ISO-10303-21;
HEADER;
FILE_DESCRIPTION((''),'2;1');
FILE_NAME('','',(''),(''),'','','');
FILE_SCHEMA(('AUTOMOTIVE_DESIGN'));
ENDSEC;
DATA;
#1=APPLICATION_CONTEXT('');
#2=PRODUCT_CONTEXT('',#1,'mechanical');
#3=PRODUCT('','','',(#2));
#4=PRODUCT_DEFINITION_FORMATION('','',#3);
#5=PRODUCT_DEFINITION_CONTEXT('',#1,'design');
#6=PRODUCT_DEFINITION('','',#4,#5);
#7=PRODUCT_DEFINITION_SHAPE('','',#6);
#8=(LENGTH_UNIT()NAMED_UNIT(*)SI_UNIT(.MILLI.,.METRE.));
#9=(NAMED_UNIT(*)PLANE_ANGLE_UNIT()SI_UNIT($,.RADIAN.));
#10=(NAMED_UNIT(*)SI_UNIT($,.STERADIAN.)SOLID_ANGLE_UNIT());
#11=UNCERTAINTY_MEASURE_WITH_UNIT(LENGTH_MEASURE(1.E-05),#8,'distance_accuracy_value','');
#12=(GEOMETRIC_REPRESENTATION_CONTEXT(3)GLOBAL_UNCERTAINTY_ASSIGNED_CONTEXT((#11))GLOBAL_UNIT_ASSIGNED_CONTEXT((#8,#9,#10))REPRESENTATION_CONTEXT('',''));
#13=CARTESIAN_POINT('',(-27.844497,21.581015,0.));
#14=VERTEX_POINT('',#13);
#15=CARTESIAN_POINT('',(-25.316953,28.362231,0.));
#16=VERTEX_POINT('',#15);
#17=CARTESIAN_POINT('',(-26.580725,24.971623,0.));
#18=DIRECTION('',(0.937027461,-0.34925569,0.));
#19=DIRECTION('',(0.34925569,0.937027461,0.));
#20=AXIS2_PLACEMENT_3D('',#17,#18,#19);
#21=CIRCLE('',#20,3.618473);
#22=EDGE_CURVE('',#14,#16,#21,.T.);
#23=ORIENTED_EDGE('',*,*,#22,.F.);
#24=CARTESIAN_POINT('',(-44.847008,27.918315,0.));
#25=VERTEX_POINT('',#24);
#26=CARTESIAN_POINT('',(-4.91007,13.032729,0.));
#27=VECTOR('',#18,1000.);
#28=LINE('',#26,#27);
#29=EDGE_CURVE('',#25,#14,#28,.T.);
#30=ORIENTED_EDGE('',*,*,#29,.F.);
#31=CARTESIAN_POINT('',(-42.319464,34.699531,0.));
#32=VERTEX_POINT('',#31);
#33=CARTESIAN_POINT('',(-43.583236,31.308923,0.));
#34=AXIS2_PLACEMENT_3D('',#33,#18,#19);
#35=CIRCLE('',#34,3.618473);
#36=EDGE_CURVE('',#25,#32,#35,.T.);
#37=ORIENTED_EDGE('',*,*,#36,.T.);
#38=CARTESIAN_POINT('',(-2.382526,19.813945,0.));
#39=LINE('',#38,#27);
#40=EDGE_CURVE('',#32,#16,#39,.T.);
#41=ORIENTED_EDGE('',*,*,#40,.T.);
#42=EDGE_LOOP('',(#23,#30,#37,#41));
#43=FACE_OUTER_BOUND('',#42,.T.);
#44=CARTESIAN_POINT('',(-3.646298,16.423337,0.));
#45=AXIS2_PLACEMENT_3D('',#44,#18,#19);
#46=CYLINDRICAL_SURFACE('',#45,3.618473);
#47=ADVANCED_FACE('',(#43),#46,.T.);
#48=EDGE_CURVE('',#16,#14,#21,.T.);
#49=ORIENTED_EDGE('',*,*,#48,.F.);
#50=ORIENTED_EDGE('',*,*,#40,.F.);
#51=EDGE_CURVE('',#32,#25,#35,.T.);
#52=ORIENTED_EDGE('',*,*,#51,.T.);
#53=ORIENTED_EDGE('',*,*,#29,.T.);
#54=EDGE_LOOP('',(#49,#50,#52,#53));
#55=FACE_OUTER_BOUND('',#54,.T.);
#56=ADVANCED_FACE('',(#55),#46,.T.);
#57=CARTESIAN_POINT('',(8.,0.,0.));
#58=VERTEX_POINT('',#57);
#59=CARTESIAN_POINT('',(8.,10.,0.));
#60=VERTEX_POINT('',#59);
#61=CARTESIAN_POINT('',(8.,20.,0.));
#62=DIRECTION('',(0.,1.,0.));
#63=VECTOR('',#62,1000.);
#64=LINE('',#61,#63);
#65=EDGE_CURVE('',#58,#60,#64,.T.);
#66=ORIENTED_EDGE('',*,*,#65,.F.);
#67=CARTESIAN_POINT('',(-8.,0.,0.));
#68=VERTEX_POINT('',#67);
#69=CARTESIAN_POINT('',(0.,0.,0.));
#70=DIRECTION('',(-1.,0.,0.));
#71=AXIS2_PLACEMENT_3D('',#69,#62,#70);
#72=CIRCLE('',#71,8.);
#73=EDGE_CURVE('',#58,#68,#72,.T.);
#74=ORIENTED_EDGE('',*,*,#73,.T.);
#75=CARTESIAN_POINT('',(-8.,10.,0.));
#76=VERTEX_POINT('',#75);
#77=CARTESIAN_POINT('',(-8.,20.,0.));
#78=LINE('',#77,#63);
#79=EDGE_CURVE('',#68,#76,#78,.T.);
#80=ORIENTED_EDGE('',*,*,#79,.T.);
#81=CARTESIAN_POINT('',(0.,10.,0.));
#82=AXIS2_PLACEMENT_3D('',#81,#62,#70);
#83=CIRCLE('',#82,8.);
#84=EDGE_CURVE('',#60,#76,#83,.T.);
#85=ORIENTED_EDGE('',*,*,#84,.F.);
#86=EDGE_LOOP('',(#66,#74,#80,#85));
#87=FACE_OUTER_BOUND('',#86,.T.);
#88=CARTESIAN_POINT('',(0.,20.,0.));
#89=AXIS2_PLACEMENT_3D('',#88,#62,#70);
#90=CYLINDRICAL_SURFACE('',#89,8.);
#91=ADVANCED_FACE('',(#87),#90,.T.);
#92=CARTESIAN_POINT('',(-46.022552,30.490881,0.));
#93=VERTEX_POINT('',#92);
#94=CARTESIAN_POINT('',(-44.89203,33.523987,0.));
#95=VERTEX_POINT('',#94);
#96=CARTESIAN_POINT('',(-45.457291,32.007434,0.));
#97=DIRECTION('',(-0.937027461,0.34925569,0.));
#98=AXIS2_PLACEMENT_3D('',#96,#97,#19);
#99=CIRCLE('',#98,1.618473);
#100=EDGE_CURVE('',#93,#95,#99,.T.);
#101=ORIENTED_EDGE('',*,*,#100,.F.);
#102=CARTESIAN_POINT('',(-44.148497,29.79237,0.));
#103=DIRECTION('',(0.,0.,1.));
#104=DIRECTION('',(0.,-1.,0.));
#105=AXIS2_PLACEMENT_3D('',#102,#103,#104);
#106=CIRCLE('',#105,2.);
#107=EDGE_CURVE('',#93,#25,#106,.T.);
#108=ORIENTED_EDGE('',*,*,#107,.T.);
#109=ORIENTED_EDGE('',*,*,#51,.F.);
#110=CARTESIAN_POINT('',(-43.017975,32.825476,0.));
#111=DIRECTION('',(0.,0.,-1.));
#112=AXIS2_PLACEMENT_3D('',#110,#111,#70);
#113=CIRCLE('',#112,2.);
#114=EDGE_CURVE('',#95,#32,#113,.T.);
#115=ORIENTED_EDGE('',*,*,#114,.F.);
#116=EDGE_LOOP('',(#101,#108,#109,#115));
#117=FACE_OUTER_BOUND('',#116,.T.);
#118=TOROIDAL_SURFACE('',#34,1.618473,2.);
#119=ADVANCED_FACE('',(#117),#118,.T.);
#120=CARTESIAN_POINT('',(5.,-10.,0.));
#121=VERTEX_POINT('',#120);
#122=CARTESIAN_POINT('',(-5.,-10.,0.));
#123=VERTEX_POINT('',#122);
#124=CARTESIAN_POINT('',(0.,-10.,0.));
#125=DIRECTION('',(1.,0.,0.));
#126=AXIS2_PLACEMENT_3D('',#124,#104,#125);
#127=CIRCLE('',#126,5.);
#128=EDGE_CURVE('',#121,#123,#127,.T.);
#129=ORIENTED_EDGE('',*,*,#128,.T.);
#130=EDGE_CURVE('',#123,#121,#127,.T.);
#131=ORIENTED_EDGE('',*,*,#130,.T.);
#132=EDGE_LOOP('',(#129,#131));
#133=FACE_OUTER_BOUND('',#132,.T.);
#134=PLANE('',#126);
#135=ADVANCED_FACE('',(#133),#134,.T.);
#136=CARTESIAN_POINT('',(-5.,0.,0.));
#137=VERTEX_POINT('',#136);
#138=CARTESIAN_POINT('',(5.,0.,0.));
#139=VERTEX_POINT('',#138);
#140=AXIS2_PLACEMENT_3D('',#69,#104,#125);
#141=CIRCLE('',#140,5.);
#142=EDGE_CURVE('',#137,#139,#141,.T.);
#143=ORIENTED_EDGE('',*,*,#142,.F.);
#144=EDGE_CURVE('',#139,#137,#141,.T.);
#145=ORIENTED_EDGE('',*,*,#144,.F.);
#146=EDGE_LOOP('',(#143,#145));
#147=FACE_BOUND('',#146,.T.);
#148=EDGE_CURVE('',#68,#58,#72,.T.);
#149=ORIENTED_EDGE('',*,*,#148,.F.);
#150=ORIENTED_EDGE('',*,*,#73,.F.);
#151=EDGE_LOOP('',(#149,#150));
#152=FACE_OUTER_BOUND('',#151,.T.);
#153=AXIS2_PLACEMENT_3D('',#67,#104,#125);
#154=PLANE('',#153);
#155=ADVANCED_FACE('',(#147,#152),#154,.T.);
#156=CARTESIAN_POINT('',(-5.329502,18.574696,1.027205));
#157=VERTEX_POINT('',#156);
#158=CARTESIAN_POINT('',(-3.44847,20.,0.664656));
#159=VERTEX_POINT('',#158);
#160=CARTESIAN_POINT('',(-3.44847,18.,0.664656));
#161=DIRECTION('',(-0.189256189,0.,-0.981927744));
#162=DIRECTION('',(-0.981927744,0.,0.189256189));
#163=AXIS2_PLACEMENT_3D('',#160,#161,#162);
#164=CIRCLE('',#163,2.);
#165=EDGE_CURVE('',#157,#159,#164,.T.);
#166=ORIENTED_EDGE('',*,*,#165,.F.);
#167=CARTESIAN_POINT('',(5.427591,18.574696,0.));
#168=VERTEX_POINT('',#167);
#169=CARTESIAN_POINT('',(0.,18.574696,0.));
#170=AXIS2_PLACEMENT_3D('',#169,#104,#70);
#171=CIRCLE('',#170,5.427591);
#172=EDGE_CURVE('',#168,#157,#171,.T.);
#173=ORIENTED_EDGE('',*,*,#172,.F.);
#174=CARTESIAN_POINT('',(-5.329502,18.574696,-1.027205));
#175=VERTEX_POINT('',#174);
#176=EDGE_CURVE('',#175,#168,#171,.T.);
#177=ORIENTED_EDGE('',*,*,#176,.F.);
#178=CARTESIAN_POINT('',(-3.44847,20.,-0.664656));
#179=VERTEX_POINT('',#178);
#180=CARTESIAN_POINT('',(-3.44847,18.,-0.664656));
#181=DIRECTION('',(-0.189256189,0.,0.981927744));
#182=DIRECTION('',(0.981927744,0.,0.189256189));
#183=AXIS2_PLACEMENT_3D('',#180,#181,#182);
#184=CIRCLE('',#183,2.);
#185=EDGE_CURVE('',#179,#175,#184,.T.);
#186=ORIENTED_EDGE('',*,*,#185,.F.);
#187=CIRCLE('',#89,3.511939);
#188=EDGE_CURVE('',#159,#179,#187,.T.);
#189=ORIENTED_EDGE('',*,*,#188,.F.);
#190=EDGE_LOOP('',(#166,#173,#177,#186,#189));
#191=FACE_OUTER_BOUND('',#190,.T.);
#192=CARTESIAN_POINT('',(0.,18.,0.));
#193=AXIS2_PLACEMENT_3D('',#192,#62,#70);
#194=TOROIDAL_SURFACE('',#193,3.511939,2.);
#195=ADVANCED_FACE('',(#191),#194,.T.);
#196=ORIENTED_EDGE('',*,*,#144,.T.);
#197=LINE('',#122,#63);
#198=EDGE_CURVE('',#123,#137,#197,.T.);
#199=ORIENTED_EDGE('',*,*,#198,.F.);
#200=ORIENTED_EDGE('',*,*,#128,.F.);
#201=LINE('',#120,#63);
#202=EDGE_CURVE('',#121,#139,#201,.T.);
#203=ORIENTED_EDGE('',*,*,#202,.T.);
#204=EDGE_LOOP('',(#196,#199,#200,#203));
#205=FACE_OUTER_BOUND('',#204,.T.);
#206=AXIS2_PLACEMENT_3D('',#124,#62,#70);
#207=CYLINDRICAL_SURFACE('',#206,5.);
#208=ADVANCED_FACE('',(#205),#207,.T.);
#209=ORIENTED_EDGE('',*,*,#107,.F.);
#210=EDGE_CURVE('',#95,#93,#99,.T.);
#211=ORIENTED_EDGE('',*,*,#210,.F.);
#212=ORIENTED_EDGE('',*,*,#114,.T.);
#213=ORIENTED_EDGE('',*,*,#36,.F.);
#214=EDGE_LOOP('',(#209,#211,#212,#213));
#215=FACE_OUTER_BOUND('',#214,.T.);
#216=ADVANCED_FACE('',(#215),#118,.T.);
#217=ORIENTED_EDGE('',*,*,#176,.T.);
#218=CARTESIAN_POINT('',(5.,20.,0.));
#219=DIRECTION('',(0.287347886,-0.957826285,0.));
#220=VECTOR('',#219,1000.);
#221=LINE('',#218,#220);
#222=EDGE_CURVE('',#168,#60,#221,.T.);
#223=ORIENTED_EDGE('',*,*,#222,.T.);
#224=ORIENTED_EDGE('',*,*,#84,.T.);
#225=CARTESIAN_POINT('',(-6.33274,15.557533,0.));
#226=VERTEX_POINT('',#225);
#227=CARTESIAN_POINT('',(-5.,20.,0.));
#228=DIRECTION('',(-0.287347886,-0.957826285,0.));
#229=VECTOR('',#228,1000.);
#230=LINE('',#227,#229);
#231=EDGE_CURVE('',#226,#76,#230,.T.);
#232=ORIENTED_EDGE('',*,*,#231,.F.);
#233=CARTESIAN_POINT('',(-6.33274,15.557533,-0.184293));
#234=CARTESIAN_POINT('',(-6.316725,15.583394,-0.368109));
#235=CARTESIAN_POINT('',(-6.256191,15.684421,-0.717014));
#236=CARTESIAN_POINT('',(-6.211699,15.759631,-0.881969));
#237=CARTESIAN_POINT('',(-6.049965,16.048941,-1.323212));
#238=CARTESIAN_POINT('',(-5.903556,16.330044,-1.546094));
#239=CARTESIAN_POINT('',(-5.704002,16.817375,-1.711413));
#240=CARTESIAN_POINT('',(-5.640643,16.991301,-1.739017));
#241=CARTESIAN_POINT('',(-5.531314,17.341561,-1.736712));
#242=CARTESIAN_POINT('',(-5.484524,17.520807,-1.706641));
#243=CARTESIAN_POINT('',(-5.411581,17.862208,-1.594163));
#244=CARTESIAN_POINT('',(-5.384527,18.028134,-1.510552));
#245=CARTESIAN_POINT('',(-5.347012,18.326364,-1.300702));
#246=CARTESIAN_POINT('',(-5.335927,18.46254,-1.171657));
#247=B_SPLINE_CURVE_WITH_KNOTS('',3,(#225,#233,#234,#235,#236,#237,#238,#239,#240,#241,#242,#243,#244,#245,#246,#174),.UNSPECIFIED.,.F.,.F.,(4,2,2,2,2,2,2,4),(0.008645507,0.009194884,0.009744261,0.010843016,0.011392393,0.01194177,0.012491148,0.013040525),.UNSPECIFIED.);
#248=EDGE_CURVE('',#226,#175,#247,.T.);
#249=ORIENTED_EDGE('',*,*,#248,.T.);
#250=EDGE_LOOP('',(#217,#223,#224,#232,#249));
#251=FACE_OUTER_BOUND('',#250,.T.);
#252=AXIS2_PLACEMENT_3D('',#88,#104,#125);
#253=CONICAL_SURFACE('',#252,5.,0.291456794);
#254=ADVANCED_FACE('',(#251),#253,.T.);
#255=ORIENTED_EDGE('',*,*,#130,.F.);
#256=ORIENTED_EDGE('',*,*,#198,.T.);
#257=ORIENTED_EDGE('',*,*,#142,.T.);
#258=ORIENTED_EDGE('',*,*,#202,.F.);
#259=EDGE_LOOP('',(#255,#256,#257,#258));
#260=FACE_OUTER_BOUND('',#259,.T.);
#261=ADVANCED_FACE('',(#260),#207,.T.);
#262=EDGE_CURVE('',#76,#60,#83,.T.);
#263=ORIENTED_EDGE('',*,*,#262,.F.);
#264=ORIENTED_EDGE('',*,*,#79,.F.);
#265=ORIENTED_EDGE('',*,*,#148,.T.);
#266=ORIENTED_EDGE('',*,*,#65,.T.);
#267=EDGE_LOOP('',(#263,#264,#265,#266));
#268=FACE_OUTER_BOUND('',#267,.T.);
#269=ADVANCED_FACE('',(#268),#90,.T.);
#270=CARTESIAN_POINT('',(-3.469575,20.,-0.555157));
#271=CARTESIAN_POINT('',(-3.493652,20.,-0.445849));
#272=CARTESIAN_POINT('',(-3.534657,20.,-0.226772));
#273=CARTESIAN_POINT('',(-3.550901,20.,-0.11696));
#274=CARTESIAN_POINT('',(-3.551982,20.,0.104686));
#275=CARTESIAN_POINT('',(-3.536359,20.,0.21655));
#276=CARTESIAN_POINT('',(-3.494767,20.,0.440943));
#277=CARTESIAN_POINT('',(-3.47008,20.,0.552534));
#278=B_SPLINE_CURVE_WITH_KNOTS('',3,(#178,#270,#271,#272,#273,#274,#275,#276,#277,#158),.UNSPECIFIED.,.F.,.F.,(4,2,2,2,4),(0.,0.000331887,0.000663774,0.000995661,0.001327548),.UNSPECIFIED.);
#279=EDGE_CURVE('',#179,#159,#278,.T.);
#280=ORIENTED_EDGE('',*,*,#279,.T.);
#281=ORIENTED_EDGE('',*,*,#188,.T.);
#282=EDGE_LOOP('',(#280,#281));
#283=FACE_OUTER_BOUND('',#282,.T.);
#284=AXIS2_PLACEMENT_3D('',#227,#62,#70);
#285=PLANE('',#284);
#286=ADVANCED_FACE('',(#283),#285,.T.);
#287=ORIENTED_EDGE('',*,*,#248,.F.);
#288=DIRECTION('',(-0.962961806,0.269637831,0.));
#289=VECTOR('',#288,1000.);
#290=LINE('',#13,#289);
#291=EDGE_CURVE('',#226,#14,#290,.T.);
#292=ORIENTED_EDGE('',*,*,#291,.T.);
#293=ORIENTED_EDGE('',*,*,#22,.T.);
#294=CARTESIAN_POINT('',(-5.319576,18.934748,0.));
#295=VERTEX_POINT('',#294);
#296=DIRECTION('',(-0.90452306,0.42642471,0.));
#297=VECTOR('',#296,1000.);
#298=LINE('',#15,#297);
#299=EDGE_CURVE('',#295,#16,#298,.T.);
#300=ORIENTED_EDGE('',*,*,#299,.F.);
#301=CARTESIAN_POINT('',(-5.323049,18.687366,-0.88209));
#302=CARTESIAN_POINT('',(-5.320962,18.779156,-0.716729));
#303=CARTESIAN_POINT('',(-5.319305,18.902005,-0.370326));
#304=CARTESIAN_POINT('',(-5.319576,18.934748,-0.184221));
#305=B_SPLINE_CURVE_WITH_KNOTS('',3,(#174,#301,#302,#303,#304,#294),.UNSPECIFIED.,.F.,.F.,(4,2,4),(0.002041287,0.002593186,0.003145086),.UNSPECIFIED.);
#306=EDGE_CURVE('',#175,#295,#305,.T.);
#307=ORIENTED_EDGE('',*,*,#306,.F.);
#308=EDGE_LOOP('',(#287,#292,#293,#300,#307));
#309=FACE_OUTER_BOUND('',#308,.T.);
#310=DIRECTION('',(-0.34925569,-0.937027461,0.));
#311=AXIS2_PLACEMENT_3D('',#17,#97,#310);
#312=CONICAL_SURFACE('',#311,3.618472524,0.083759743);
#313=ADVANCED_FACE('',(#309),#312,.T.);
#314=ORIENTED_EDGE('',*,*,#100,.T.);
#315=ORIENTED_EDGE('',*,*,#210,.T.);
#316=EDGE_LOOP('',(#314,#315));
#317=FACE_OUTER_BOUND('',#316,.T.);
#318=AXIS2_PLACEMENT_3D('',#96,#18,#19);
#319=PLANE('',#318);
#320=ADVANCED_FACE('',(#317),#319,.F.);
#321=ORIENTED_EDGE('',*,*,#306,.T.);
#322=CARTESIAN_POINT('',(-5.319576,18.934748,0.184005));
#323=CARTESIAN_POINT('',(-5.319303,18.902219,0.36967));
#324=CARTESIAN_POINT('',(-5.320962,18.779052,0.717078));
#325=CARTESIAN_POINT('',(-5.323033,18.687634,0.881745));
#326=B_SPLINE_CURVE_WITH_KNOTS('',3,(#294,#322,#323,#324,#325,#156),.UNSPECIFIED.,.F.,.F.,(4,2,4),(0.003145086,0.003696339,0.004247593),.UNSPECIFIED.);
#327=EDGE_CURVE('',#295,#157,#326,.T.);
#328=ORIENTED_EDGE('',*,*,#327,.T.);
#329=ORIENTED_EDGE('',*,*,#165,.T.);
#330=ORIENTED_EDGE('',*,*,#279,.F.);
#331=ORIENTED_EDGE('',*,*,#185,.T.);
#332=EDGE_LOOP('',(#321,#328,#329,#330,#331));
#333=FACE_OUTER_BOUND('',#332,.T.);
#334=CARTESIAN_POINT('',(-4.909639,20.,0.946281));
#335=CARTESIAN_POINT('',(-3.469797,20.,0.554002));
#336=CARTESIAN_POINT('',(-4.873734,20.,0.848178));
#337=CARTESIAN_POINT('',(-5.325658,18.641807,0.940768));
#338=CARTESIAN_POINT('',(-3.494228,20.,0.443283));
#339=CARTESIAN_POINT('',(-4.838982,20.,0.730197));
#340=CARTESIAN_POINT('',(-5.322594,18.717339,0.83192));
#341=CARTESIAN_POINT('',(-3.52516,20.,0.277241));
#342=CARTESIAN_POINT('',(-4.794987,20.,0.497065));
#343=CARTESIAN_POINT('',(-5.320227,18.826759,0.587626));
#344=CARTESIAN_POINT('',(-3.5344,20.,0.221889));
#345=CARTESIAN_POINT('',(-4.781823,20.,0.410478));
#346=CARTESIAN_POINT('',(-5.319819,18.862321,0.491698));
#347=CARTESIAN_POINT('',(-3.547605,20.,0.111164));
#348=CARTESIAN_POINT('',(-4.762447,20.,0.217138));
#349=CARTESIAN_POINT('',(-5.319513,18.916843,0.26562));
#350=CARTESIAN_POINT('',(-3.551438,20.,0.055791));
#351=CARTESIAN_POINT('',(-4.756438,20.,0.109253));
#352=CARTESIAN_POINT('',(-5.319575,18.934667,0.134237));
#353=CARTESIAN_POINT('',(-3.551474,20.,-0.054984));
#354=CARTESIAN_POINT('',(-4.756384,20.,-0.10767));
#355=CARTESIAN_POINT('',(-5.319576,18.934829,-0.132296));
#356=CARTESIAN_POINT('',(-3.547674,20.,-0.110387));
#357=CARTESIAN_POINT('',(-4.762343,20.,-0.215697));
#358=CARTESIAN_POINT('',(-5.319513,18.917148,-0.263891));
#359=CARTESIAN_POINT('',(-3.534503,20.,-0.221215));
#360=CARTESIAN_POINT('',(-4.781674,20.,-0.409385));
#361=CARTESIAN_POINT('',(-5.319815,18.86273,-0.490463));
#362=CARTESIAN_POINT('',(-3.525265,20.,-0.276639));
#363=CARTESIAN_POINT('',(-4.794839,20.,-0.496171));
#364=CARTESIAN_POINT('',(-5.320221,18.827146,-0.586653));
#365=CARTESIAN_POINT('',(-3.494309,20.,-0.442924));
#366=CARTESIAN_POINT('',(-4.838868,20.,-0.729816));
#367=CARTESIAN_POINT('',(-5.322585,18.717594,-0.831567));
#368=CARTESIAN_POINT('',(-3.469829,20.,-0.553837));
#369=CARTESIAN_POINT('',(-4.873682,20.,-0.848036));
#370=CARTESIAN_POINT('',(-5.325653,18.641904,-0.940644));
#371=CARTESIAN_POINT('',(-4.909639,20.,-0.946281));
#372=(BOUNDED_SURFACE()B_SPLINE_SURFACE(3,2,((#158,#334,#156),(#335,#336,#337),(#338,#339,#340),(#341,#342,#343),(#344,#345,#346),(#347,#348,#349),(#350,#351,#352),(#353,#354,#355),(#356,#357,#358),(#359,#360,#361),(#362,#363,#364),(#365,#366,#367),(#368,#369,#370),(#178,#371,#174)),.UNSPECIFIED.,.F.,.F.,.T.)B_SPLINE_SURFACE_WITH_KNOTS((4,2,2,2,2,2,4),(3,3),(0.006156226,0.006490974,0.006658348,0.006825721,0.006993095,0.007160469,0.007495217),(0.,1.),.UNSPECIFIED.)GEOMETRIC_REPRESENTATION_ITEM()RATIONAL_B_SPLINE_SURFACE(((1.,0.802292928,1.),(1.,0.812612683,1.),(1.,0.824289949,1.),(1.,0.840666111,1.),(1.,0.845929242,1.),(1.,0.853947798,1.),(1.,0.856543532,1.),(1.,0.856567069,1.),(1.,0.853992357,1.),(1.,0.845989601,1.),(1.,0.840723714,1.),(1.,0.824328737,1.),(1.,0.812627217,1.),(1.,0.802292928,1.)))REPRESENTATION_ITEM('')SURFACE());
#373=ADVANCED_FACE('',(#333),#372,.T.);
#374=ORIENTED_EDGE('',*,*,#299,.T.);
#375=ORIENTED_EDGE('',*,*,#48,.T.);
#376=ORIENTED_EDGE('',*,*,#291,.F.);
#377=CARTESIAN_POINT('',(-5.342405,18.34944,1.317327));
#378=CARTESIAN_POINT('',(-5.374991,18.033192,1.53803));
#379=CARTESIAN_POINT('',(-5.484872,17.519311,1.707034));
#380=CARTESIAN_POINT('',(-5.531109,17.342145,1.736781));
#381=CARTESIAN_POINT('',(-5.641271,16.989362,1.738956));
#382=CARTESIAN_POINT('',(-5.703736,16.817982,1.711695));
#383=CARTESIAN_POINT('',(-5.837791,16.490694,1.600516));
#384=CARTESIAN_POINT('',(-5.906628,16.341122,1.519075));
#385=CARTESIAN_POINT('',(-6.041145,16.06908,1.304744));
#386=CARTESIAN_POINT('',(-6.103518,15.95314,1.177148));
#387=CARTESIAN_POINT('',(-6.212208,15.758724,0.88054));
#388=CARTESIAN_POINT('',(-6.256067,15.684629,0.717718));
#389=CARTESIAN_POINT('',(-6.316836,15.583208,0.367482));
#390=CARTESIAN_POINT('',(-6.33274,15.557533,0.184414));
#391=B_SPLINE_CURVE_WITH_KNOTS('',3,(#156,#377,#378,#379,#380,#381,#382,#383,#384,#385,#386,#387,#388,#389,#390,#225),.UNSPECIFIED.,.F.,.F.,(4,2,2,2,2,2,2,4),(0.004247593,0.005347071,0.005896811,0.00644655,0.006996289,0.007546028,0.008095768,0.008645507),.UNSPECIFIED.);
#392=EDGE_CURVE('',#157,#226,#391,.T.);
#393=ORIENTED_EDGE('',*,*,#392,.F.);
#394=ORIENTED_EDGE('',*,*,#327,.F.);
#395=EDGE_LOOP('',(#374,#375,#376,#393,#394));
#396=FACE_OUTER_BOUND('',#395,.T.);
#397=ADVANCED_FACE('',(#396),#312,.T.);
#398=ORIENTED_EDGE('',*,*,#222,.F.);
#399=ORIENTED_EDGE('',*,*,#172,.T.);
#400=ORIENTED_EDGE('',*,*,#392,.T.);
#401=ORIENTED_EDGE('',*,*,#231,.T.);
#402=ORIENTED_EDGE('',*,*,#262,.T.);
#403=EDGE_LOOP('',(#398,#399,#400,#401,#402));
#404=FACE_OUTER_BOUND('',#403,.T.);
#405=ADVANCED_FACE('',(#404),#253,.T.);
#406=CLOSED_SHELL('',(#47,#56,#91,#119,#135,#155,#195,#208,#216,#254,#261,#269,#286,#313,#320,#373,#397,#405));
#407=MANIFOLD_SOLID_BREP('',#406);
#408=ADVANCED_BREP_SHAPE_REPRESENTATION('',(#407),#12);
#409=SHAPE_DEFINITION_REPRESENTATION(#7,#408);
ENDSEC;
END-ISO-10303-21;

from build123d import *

# Parameters (mm, degrees)
SKETCH4_R           = 5
BOSS_EXTRUDE1_DEPTH = 10
FILLET1_R           = 2


with BuildPart() as part:
    # Sketch2 → Revolve1 (revolve)
    with BuildSketch(Plane.XY):
        Polygon((0, 0), (0, 10), (0, 20), (-5, 20), (-8, 10), (-8, 0), align=None)
    revolve(axis=Axis((0, 20, 0), (0, -1, 0)))

    # Sketch3 → Revolve2 (revolve)
    with BuildSketch(Plane.XY, mode=Mode.PRIVATE) as revolve2_sk:
        Polygon((-45.457291118, 32.007434158), (-46.721063236, 28.616826036), (-27.844496784, 21.581014904), (-4.192388941, 14.958215321), (-3.646298208, 16.423336801), align=None)
    revolve(revolve2_sk.sketch.rotate(Axis((-3.646298208, 16.423336801, 0), (-0.9370274611537507, 0.34925569006639867, 0)), 180), axis=Axis((-3.646298208, 16.423336801, 0), (-0.9370274611537507, 0.34925569006639867, 0)))

    # Sketch4 → Boss-Extrude1 (add)
    with BuildSketch(Plane.XZ):
        Circle(SKETCH4_R)
    extrude(amount=BOSS_EXTRUDE1_DEPTH)

    # Fillet1
    fillet1_edges = [part.edges().sort_by_distance(p)[0] for p in [
        (-46.721063236, 28.616826036, 0),
        (5, 20, 0),
    ]]
    fillet(fillet1_edges, radius=FILLET1_R)


solid = part.part
